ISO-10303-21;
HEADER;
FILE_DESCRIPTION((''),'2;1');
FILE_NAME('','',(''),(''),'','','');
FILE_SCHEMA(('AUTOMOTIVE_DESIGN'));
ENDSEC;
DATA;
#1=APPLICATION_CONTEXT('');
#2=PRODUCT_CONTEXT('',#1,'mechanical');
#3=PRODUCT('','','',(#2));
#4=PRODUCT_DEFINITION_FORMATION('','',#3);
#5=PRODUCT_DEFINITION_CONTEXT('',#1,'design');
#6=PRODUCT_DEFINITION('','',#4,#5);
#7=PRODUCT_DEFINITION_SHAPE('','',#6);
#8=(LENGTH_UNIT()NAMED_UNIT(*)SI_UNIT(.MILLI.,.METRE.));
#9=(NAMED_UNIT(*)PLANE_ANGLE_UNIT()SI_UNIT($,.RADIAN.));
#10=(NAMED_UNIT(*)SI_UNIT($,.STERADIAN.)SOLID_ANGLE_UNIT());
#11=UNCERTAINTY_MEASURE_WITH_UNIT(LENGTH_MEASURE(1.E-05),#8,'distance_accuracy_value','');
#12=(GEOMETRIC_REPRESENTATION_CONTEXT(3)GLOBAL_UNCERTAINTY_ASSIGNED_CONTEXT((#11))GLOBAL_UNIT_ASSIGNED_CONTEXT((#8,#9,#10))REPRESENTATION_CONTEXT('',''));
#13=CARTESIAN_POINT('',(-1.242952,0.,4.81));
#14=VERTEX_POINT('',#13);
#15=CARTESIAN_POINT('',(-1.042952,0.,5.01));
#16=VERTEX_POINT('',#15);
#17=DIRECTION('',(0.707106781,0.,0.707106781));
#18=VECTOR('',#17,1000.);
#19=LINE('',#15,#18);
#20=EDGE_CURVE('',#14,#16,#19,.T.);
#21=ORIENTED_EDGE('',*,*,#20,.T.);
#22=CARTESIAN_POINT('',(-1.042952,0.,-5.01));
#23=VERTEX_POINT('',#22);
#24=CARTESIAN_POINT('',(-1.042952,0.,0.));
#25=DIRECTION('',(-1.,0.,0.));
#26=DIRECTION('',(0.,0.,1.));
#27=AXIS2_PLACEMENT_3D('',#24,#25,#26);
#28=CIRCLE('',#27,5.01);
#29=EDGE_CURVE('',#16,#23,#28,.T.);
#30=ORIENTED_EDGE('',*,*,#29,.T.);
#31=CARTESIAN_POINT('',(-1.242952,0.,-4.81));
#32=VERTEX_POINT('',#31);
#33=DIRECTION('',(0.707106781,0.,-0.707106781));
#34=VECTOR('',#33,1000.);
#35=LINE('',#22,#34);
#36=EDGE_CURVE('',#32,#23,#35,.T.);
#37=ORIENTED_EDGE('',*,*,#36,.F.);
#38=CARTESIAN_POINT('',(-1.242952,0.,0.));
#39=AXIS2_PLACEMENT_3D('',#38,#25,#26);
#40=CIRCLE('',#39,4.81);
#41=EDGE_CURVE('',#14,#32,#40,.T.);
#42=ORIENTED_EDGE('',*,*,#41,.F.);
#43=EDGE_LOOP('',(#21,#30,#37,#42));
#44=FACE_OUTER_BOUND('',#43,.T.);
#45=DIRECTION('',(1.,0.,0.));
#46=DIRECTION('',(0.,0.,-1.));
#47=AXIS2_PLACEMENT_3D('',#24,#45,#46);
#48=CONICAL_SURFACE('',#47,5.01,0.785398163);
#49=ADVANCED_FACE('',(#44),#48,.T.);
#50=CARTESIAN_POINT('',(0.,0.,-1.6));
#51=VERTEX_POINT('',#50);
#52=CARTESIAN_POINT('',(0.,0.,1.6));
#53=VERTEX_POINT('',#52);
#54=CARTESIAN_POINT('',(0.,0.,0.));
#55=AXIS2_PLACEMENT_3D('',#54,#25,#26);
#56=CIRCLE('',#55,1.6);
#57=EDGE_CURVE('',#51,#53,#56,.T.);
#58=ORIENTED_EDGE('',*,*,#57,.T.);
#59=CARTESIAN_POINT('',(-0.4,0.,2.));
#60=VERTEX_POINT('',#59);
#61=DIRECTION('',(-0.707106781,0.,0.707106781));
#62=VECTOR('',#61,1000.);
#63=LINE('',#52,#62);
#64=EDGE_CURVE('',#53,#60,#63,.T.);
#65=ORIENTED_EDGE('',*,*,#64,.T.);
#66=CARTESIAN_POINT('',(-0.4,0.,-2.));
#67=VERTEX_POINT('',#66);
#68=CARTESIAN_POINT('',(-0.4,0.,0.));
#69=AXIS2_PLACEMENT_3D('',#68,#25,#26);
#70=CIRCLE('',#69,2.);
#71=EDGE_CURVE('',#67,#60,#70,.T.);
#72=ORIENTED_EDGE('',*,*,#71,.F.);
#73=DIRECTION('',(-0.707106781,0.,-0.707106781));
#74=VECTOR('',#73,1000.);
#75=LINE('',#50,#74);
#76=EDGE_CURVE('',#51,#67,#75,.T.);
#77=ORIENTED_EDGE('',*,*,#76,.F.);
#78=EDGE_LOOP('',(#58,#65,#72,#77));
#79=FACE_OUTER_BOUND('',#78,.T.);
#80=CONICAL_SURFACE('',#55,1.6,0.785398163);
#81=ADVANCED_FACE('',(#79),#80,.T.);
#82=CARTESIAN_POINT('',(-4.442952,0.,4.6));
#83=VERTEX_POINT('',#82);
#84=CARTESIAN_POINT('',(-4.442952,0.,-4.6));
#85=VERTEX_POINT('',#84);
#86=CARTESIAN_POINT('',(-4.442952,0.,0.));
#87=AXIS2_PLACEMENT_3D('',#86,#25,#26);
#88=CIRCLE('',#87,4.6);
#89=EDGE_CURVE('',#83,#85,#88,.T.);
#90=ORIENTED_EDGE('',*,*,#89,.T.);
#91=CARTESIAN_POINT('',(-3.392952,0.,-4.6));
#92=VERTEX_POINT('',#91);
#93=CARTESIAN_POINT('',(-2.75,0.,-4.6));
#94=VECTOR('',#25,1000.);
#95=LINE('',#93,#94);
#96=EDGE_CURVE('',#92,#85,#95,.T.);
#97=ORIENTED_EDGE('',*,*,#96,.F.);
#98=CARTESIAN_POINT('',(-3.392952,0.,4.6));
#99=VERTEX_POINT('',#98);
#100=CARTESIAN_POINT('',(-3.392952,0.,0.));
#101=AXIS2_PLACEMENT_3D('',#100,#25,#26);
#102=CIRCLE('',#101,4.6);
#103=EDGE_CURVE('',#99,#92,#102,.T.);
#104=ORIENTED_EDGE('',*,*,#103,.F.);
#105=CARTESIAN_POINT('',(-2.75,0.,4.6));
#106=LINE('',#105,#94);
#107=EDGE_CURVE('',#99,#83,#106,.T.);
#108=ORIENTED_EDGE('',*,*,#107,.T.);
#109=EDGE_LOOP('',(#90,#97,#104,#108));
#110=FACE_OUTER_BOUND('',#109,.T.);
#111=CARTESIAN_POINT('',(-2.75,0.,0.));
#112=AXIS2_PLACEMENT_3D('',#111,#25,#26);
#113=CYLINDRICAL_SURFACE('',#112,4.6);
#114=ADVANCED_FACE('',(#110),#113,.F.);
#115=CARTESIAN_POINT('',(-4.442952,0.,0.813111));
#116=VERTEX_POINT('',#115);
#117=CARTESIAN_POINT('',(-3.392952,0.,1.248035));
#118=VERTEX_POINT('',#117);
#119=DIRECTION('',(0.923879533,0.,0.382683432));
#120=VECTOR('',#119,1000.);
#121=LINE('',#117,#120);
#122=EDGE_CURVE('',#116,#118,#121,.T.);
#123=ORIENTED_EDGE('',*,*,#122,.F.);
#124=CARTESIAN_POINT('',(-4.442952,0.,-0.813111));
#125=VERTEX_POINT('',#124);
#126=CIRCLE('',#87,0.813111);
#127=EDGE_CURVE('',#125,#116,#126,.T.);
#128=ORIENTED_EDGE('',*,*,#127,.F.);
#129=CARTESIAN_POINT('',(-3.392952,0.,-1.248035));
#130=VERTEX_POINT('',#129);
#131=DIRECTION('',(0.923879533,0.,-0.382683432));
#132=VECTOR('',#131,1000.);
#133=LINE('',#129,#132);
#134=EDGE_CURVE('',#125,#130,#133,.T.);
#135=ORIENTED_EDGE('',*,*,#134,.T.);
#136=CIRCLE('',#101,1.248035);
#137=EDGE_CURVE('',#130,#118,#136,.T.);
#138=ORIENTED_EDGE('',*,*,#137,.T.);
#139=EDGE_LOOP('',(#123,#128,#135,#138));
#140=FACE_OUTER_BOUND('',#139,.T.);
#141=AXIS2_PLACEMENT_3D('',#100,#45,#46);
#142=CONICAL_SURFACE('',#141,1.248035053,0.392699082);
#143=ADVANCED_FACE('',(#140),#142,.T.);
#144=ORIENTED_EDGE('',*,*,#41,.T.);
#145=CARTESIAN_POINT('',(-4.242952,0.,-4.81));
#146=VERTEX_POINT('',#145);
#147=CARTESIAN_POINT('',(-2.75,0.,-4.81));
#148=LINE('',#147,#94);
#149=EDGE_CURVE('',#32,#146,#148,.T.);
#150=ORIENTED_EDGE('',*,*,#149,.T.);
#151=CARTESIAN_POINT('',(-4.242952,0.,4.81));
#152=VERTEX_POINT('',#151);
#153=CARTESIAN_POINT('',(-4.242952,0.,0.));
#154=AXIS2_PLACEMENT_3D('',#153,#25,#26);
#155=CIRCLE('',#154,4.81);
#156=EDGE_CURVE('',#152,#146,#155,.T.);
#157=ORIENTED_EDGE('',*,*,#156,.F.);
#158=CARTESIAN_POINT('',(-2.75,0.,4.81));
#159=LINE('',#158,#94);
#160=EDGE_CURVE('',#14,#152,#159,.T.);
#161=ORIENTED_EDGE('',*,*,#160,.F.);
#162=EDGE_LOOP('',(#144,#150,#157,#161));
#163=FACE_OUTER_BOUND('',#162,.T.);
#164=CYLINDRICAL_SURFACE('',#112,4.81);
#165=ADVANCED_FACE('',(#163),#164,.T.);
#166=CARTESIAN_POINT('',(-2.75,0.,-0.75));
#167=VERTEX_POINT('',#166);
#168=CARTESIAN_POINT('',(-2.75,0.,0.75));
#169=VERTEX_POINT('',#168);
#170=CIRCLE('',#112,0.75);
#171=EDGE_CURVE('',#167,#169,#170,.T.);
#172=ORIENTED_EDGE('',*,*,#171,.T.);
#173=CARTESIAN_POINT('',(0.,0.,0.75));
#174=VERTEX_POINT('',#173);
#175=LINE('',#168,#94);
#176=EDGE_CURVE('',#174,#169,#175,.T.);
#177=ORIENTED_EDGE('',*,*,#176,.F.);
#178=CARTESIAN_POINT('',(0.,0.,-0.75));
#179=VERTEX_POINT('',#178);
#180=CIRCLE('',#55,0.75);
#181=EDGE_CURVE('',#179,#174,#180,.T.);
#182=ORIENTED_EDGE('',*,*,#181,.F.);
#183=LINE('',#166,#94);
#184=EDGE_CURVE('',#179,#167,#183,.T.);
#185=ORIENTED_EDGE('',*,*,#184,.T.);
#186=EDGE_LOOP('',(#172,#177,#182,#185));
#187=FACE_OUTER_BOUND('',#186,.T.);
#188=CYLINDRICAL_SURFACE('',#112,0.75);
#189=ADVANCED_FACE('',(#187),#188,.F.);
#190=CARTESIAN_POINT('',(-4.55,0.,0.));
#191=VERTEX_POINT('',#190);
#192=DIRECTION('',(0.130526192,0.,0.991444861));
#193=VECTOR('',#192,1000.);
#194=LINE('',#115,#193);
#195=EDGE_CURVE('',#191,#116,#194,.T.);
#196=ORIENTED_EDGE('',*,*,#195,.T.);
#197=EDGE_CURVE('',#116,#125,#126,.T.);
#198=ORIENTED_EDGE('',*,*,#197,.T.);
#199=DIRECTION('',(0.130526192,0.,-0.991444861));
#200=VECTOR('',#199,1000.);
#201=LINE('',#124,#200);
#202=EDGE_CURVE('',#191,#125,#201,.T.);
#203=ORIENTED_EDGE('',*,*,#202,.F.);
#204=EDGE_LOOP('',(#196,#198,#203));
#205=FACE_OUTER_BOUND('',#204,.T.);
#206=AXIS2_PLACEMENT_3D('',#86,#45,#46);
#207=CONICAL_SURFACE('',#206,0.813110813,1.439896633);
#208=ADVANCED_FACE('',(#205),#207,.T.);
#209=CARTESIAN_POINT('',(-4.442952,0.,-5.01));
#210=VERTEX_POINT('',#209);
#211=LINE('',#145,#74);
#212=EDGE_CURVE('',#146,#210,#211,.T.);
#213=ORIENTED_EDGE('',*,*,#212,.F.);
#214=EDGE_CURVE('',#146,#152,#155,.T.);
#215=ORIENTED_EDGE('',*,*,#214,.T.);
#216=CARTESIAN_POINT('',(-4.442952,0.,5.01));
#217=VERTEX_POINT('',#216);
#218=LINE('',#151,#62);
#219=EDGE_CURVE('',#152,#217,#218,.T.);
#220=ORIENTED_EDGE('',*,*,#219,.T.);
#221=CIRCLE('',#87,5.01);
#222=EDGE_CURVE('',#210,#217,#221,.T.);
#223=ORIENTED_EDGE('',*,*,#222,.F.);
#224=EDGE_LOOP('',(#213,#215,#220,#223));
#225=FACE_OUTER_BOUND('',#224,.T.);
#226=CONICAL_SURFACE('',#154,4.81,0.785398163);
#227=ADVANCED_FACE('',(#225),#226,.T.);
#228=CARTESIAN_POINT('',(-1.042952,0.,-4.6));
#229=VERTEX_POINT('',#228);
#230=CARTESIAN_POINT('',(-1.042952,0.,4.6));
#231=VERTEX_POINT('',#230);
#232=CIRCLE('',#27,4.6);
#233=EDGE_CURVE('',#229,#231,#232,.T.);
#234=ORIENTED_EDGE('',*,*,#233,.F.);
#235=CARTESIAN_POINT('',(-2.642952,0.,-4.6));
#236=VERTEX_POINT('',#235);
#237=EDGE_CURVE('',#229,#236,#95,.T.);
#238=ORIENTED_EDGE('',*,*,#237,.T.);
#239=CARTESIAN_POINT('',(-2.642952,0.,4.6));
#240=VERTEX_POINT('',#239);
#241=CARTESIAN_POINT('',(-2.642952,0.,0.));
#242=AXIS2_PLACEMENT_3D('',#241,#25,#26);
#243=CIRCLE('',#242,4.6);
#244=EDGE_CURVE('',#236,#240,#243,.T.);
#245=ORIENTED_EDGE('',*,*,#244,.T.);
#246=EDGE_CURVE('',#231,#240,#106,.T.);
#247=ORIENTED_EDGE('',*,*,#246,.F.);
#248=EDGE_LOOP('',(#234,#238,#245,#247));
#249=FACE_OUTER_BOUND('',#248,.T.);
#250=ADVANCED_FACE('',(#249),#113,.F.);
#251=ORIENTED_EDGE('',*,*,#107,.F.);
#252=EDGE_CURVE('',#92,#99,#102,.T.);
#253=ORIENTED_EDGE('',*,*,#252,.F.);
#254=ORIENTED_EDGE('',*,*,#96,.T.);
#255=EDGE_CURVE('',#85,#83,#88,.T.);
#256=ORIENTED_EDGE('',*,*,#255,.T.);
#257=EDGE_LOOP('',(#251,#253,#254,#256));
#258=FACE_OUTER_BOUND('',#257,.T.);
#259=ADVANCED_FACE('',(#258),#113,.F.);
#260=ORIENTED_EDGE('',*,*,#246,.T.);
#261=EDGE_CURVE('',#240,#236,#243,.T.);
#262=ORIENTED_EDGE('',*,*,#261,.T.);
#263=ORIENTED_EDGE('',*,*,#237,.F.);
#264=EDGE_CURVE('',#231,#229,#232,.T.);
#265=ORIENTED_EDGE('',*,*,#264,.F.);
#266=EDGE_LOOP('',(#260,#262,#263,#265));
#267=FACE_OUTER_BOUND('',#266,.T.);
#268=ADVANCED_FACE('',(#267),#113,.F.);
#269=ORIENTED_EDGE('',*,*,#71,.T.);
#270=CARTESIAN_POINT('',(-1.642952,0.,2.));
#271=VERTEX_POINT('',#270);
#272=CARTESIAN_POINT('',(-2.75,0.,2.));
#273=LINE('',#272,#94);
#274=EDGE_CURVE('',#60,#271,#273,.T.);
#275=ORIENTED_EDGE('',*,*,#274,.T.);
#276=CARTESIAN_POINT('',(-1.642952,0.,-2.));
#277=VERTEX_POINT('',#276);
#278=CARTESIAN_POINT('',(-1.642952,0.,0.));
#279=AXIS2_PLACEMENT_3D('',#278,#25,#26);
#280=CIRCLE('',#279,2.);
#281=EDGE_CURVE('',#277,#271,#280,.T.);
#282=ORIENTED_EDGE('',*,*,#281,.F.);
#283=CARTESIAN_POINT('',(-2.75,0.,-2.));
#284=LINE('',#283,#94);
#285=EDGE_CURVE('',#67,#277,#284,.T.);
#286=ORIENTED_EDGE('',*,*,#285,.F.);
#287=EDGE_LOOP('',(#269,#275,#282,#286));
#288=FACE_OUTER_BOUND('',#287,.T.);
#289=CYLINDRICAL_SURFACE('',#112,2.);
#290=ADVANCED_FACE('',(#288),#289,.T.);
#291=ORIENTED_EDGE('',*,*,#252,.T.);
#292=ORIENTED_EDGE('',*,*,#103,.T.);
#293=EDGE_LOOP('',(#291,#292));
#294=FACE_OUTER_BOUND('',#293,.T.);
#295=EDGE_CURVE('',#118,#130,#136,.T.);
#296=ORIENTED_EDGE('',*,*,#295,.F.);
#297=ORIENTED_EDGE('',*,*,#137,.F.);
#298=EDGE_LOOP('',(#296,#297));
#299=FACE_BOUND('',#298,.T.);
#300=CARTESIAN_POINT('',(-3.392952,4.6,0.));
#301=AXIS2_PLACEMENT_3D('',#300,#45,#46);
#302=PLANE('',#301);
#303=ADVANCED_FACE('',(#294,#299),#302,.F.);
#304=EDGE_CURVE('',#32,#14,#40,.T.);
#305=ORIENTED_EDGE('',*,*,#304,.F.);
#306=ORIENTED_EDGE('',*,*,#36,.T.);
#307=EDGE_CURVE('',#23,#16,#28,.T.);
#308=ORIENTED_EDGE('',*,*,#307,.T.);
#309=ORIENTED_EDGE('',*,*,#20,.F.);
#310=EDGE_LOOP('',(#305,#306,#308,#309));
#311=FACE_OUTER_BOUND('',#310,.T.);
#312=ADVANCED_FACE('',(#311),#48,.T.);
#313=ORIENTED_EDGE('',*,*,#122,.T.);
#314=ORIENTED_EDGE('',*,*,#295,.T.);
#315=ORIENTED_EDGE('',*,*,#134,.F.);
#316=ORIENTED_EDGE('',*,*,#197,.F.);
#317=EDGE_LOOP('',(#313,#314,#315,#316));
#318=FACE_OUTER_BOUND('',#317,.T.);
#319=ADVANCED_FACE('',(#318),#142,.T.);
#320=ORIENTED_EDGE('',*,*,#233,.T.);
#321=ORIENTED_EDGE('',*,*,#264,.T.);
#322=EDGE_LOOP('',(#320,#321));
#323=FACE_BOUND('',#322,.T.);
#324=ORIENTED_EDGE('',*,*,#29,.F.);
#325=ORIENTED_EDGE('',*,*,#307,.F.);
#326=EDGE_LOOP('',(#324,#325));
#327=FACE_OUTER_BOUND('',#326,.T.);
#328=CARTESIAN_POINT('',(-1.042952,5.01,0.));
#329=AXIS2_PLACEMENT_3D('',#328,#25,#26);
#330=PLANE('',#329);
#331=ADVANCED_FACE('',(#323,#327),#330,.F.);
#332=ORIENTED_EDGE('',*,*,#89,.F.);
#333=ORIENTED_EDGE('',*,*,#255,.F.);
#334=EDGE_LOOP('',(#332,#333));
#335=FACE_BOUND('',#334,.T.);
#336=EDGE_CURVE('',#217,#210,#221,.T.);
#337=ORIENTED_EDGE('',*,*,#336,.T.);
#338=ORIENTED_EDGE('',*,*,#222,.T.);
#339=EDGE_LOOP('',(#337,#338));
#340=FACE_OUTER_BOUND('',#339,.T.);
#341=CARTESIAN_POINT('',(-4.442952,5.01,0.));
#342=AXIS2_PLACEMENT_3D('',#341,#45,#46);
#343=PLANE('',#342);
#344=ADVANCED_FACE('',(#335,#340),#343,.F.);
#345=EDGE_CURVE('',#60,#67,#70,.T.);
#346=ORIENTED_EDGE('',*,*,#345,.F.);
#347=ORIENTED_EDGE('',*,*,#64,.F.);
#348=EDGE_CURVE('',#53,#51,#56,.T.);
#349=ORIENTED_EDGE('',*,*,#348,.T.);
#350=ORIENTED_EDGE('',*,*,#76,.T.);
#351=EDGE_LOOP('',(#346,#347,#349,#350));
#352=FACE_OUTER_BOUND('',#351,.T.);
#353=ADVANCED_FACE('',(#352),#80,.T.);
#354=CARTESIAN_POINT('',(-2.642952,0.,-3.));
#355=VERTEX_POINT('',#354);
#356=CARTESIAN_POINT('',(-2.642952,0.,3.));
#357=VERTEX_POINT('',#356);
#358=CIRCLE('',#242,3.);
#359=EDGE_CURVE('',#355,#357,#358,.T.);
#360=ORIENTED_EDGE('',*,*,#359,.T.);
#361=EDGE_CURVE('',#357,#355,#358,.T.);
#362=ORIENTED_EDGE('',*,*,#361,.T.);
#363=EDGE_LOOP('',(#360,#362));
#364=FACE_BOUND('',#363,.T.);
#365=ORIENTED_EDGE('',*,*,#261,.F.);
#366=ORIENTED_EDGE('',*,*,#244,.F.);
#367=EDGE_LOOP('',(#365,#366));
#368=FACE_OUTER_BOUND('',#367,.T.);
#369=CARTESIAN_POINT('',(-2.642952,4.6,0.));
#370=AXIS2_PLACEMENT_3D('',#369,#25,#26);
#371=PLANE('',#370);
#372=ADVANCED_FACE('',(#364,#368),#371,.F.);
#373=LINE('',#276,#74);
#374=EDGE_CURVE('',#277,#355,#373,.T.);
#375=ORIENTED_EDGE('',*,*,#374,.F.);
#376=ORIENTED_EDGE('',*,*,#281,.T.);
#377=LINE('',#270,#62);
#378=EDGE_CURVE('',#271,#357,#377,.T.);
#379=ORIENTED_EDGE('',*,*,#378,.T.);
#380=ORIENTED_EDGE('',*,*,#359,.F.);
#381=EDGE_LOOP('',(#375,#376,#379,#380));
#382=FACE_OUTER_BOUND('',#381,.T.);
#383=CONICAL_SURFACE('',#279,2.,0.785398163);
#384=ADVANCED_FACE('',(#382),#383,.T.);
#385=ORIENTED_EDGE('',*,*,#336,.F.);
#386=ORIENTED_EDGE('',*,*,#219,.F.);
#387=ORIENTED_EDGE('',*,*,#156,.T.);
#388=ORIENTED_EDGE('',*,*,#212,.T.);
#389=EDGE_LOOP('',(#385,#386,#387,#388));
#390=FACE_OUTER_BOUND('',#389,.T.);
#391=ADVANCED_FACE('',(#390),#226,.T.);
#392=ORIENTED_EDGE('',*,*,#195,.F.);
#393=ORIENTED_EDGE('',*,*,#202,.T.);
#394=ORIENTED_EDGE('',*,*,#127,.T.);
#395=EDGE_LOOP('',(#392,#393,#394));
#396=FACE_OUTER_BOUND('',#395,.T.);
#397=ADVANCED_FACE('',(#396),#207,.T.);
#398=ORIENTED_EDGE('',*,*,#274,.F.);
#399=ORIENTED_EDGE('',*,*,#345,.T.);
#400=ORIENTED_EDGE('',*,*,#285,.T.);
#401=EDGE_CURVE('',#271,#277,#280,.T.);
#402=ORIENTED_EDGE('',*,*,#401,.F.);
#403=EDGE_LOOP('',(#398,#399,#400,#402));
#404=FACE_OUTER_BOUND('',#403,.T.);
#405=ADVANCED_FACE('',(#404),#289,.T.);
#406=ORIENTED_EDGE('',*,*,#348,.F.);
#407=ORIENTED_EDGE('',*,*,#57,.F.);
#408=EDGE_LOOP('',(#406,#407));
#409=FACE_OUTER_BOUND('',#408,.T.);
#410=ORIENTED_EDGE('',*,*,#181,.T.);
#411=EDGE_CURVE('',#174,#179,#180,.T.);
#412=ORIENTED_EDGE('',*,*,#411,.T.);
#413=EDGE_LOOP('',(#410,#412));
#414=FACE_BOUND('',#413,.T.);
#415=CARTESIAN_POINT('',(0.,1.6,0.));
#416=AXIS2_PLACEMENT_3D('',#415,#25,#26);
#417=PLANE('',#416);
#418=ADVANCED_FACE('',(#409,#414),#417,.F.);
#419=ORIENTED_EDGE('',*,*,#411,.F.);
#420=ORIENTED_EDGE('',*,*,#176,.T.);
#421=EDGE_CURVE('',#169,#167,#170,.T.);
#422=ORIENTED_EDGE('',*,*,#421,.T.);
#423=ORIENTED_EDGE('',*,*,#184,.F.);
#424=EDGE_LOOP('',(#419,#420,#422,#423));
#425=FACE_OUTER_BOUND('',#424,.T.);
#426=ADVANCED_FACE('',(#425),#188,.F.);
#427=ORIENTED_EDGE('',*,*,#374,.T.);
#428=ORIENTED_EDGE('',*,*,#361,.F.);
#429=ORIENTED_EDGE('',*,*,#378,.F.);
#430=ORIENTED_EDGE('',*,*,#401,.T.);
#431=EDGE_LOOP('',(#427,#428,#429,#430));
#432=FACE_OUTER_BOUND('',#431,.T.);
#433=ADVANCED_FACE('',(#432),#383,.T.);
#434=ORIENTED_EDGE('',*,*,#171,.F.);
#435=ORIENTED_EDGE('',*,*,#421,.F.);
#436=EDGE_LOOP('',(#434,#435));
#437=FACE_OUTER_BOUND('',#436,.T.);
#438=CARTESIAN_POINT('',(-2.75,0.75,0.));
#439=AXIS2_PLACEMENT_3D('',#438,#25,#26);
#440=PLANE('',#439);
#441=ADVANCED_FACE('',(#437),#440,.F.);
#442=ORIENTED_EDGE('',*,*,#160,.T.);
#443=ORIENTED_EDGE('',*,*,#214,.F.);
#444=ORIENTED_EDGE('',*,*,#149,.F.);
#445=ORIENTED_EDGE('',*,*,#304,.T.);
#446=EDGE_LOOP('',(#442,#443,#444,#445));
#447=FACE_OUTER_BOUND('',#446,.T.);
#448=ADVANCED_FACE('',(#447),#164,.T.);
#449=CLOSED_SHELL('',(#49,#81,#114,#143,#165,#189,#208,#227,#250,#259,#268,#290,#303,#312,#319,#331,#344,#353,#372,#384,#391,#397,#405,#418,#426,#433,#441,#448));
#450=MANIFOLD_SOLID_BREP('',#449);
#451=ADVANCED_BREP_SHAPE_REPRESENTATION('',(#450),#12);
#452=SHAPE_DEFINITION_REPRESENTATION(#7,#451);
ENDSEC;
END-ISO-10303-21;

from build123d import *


with BuildPart() as part:
    # Sketch1 → Revolve1 (revolve)
    with BuildSketch(Plane.XY, mode=Mode.PRIVATE) as revolve1_sk:
        Polygon((-4.442951931, 5.01), (-4.442951931, 4.6), (-3.392951931, 4.6), (-3.392951931, 1.248035053), (-4.442951931, 0.813110813), (-4.55, 0), (-2.75, 0), (-2.75, 0.75), (0, 0.75), (0, 1.6), (-0.4, 2), (-1.642951931, 2), (-2.642951931, 3), (-2.642951931, 4.6), (-1.042951931, 4.6), (-1.042951931, 5.01), (-1.242951931, 4.81), (-4.242951931, 4.81), align=None)
    revolve(revolve1_sk.sketch.rotate(Axis((-2.75, 0, 0), (1, 0, 0)), 90), axis=Axis((-2.75, 0, 0), (1, 0, 0)))


solid = part.part
